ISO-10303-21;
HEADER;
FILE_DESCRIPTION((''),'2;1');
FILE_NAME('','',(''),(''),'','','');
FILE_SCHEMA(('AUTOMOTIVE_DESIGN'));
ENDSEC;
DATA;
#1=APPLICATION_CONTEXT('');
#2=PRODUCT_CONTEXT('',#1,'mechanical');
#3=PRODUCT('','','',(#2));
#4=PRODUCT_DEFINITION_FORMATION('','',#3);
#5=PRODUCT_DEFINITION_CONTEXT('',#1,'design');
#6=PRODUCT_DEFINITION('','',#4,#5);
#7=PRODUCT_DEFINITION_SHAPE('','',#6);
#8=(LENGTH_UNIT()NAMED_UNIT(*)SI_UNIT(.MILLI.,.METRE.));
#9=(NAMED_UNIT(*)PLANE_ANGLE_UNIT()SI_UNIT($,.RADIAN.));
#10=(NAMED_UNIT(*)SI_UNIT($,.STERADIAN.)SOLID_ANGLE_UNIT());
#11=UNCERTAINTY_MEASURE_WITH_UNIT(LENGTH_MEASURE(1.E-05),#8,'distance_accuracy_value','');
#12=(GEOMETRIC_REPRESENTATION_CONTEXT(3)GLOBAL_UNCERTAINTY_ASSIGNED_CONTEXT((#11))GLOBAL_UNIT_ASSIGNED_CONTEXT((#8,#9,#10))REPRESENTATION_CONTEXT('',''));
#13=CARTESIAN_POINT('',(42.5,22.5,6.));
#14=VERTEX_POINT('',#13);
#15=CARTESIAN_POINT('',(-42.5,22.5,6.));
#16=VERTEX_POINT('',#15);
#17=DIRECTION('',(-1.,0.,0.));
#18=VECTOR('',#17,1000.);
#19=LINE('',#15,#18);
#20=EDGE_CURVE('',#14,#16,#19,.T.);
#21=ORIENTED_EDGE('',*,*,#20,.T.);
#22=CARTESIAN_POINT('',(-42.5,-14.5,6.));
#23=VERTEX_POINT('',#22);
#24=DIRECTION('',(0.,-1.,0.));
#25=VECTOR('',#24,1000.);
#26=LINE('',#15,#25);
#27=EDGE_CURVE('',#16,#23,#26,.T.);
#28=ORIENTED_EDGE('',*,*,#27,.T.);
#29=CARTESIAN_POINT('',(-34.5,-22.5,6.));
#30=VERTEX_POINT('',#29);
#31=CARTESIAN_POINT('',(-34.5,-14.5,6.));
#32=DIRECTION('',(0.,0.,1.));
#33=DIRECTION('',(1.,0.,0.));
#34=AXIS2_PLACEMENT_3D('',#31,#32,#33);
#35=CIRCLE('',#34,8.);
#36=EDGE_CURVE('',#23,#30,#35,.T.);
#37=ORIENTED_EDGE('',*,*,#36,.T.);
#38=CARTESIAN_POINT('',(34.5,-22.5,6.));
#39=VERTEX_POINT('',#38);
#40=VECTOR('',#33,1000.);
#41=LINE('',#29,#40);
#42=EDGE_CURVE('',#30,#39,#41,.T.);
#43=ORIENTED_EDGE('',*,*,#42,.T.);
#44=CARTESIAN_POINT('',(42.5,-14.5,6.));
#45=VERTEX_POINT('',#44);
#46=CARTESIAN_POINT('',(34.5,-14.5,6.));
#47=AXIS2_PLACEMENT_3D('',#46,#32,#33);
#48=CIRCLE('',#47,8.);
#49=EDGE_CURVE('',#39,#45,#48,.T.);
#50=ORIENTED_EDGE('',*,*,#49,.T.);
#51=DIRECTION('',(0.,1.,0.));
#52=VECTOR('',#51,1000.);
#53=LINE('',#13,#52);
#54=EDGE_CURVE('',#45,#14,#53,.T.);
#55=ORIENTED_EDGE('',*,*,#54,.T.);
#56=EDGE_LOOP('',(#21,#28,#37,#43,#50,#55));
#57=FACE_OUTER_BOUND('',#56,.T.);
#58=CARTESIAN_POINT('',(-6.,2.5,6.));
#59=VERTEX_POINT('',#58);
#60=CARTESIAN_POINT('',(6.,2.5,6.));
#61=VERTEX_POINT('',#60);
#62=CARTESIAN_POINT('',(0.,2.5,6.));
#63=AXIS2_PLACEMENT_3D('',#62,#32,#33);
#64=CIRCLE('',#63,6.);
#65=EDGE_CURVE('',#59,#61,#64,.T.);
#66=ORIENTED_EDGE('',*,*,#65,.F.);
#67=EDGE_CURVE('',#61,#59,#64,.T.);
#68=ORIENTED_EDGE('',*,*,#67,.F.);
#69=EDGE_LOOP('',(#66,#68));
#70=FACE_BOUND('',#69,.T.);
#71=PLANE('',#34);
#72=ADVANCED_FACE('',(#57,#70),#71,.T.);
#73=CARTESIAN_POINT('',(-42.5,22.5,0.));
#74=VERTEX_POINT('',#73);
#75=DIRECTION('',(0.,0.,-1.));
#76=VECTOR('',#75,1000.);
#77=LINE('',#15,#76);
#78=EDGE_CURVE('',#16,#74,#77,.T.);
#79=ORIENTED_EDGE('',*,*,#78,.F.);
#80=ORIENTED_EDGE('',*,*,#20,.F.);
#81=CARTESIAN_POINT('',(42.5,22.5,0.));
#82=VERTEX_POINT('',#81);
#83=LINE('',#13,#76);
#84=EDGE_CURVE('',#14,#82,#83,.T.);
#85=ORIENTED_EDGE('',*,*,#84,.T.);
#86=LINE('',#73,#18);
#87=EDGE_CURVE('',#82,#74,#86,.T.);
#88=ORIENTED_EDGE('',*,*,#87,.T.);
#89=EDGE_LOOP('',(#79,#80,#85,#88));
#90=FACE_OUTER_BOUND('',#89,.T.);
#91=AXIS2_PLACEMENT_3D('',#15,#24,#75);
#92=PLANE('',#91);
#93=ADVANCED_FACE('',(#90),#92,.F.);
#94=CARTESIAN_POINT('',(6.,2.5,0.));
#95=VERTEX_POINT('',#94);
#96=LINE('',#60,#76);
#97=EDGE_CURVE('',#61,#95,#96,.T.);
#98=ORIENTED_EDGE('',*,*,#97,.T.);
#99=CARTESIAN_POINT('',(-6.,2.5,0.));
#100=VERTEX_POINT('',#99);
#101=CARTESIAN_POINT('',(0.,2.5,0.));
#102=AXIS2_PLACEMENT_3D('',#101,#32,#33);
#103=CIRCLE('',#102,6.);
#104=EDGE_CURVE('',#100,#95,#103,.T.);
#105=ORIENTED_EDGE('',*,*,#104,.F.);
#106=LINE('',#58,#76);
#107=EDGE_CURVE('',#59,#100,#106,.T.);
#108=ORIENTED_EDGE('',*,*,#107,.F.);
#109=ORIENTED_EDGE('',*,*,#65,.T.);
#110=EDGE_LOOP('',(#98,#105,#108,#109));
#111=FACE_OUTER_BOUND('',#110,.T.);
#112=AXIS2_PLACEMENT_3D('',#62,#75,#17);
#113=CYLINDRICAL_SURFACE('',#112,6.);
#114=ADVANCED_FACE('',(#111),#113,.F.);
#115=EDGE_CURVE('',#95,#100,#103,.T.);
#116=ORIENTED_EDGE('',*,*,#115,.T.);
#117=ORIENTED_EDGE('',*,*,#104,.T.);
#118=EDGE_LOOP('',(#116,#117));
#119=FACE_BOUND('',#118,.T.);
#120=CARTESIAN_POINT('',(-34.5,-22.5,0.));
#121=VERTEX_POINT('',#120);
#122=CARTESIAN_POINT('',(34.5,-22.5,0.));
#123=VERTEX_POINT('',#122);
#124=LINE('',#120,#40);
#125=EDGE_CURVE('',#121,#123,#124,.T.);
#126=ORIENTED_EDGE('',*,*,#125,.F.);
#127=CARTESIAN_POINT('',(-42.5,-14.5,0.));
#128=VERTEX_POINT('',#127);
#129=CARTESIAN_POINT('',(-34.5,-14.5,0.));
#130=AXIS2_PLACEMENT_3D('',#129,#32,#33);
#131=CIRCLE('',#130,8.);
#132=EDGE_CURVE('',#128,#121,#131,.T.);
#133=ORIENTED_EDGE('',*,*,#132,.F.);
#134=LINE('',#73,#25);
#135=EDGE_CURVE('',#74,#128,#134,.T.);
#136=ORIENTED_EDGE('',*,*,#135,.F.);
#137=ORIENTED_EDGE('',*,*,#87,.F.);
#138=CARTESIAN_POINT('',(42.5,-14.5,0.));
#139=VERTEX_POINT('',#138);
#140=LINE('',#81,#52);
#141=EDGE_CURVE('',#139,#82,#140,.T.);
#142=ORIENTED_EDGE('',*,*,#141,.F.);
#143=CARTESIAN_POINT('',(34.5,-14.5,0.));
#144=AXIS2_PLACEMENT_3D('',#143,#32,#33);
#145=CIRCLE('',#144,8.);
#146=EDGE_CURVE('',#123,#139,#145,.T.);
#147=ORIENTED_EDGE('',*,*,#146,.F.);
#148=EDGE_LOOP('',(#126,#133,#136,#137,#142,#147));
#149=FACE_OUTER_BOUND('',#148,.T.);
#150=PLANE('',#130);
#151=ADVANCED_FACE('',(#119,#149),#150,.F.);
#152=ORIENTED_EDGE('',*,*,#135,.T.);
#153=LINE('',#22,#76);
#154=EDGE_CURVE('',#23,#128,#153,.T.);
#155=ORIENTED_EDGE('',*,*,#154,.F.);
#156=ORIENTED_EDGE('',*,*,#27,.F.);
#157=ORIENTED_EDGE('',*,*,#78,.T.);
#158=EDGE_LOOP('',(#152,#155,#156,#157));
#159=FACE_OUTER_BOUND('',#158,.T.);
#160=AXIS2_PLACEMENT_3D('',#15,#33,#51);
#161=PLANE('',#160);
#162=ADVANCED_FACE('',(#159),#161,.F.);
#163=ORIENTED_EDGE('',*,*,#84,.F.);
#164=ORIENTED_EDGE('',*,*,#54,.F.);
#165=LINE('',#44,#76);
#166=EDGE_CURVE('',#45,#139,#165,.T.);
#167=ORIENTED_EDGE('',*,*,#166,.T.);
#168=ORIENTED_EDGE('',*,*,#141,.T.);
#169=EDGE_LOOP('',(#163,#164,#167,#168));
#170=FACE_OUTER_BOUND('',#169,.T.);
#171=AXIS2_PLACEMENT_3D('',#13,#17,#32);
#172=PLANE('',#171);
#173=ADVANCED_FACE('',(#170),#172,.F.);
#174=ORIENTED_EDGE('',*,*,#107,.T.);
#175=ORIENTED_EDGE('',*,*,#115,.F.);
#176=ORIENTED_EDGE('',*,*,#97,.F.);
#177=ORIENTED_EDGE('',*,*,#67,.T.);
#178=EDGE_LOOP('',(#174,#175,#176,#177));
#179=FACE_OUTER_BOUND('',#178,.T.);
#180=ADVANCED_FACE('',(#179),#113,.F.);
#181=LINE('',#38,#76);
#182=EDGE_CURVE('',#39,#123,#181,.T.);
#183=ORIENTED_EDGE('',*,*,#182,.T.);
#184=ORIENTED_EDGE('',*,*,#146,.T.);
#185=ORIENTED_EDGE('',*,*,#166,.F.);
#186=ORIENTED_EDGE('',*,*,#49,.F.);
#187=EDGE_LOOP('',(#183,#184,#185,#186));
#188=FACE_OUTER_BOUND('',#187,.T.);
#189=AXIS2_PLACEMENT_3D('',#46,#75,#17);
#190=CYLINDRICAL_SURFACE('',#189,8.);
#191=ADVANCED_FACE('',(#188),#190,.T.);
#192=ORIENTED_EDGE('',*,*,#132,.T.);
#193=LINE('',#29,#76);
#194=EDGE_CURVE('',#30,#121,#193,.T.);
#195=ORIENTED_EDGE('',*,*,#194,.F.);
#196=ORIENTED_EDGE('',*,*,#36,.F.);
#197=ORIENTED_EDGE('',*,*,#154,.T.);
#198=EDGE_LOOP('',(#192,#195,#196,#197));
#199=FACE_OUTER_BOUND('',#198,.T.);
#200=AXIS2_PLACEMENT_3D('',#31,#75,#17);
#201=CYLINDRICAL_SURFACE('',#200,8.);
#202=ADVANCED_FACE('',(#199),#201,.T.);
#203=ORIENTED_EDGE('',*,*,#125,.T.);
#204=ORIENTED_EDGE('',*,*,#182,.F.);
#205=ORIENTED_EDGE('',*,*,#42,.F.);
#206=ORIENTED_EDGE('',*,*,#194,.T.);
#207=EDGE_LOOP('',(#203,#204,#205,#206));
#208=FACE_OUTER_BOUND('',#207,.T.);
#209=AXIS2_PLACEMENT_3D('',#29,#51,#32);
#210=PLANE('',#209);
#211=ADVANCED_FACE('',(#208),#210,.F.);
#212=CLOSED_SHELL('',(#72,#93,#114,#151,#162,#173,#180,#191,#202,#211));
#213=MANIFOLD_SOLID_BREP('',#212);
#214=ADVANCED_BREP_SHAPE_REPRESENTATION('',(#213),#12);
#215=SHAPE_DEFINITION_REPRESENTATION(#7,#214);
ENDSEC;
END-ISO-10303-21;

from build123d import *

# Parameters (mm, degrees)
SKETCH_1_R      = 6
EXTRUDE_1_DEPTH = 6


with BuildPart() as part:
    # 草图1 → 凸台-拉伸1 (new body)
    with BuildSketch(Plane.XY):
        with BuildLine():
            Line((-42.5, 22.5), (42.5, 22.5))
            Line((42.5, 22.5), (42.5, -14.5))
            ThreePointArc((42.5, -14.5), (40.156854249, -20.156854249), (34.5, -22.5))
            Line((34.5, -22.5), (-34.5, -22.5))
            ThreePointArc((-34.5, -22.5), (-40.156854249, -20.156854249), (-42.5, -14.5))
            Line((-42.5, -14.5), (-42.5, 22.5))
        make_face()
        with Locations((0, 2.5)):
            Circle(SKETCH_1_R, mode=Mode.SUBTRACT)
    extrude(amount=EXTRUDE_1_DEPTH)


solid = part.part
